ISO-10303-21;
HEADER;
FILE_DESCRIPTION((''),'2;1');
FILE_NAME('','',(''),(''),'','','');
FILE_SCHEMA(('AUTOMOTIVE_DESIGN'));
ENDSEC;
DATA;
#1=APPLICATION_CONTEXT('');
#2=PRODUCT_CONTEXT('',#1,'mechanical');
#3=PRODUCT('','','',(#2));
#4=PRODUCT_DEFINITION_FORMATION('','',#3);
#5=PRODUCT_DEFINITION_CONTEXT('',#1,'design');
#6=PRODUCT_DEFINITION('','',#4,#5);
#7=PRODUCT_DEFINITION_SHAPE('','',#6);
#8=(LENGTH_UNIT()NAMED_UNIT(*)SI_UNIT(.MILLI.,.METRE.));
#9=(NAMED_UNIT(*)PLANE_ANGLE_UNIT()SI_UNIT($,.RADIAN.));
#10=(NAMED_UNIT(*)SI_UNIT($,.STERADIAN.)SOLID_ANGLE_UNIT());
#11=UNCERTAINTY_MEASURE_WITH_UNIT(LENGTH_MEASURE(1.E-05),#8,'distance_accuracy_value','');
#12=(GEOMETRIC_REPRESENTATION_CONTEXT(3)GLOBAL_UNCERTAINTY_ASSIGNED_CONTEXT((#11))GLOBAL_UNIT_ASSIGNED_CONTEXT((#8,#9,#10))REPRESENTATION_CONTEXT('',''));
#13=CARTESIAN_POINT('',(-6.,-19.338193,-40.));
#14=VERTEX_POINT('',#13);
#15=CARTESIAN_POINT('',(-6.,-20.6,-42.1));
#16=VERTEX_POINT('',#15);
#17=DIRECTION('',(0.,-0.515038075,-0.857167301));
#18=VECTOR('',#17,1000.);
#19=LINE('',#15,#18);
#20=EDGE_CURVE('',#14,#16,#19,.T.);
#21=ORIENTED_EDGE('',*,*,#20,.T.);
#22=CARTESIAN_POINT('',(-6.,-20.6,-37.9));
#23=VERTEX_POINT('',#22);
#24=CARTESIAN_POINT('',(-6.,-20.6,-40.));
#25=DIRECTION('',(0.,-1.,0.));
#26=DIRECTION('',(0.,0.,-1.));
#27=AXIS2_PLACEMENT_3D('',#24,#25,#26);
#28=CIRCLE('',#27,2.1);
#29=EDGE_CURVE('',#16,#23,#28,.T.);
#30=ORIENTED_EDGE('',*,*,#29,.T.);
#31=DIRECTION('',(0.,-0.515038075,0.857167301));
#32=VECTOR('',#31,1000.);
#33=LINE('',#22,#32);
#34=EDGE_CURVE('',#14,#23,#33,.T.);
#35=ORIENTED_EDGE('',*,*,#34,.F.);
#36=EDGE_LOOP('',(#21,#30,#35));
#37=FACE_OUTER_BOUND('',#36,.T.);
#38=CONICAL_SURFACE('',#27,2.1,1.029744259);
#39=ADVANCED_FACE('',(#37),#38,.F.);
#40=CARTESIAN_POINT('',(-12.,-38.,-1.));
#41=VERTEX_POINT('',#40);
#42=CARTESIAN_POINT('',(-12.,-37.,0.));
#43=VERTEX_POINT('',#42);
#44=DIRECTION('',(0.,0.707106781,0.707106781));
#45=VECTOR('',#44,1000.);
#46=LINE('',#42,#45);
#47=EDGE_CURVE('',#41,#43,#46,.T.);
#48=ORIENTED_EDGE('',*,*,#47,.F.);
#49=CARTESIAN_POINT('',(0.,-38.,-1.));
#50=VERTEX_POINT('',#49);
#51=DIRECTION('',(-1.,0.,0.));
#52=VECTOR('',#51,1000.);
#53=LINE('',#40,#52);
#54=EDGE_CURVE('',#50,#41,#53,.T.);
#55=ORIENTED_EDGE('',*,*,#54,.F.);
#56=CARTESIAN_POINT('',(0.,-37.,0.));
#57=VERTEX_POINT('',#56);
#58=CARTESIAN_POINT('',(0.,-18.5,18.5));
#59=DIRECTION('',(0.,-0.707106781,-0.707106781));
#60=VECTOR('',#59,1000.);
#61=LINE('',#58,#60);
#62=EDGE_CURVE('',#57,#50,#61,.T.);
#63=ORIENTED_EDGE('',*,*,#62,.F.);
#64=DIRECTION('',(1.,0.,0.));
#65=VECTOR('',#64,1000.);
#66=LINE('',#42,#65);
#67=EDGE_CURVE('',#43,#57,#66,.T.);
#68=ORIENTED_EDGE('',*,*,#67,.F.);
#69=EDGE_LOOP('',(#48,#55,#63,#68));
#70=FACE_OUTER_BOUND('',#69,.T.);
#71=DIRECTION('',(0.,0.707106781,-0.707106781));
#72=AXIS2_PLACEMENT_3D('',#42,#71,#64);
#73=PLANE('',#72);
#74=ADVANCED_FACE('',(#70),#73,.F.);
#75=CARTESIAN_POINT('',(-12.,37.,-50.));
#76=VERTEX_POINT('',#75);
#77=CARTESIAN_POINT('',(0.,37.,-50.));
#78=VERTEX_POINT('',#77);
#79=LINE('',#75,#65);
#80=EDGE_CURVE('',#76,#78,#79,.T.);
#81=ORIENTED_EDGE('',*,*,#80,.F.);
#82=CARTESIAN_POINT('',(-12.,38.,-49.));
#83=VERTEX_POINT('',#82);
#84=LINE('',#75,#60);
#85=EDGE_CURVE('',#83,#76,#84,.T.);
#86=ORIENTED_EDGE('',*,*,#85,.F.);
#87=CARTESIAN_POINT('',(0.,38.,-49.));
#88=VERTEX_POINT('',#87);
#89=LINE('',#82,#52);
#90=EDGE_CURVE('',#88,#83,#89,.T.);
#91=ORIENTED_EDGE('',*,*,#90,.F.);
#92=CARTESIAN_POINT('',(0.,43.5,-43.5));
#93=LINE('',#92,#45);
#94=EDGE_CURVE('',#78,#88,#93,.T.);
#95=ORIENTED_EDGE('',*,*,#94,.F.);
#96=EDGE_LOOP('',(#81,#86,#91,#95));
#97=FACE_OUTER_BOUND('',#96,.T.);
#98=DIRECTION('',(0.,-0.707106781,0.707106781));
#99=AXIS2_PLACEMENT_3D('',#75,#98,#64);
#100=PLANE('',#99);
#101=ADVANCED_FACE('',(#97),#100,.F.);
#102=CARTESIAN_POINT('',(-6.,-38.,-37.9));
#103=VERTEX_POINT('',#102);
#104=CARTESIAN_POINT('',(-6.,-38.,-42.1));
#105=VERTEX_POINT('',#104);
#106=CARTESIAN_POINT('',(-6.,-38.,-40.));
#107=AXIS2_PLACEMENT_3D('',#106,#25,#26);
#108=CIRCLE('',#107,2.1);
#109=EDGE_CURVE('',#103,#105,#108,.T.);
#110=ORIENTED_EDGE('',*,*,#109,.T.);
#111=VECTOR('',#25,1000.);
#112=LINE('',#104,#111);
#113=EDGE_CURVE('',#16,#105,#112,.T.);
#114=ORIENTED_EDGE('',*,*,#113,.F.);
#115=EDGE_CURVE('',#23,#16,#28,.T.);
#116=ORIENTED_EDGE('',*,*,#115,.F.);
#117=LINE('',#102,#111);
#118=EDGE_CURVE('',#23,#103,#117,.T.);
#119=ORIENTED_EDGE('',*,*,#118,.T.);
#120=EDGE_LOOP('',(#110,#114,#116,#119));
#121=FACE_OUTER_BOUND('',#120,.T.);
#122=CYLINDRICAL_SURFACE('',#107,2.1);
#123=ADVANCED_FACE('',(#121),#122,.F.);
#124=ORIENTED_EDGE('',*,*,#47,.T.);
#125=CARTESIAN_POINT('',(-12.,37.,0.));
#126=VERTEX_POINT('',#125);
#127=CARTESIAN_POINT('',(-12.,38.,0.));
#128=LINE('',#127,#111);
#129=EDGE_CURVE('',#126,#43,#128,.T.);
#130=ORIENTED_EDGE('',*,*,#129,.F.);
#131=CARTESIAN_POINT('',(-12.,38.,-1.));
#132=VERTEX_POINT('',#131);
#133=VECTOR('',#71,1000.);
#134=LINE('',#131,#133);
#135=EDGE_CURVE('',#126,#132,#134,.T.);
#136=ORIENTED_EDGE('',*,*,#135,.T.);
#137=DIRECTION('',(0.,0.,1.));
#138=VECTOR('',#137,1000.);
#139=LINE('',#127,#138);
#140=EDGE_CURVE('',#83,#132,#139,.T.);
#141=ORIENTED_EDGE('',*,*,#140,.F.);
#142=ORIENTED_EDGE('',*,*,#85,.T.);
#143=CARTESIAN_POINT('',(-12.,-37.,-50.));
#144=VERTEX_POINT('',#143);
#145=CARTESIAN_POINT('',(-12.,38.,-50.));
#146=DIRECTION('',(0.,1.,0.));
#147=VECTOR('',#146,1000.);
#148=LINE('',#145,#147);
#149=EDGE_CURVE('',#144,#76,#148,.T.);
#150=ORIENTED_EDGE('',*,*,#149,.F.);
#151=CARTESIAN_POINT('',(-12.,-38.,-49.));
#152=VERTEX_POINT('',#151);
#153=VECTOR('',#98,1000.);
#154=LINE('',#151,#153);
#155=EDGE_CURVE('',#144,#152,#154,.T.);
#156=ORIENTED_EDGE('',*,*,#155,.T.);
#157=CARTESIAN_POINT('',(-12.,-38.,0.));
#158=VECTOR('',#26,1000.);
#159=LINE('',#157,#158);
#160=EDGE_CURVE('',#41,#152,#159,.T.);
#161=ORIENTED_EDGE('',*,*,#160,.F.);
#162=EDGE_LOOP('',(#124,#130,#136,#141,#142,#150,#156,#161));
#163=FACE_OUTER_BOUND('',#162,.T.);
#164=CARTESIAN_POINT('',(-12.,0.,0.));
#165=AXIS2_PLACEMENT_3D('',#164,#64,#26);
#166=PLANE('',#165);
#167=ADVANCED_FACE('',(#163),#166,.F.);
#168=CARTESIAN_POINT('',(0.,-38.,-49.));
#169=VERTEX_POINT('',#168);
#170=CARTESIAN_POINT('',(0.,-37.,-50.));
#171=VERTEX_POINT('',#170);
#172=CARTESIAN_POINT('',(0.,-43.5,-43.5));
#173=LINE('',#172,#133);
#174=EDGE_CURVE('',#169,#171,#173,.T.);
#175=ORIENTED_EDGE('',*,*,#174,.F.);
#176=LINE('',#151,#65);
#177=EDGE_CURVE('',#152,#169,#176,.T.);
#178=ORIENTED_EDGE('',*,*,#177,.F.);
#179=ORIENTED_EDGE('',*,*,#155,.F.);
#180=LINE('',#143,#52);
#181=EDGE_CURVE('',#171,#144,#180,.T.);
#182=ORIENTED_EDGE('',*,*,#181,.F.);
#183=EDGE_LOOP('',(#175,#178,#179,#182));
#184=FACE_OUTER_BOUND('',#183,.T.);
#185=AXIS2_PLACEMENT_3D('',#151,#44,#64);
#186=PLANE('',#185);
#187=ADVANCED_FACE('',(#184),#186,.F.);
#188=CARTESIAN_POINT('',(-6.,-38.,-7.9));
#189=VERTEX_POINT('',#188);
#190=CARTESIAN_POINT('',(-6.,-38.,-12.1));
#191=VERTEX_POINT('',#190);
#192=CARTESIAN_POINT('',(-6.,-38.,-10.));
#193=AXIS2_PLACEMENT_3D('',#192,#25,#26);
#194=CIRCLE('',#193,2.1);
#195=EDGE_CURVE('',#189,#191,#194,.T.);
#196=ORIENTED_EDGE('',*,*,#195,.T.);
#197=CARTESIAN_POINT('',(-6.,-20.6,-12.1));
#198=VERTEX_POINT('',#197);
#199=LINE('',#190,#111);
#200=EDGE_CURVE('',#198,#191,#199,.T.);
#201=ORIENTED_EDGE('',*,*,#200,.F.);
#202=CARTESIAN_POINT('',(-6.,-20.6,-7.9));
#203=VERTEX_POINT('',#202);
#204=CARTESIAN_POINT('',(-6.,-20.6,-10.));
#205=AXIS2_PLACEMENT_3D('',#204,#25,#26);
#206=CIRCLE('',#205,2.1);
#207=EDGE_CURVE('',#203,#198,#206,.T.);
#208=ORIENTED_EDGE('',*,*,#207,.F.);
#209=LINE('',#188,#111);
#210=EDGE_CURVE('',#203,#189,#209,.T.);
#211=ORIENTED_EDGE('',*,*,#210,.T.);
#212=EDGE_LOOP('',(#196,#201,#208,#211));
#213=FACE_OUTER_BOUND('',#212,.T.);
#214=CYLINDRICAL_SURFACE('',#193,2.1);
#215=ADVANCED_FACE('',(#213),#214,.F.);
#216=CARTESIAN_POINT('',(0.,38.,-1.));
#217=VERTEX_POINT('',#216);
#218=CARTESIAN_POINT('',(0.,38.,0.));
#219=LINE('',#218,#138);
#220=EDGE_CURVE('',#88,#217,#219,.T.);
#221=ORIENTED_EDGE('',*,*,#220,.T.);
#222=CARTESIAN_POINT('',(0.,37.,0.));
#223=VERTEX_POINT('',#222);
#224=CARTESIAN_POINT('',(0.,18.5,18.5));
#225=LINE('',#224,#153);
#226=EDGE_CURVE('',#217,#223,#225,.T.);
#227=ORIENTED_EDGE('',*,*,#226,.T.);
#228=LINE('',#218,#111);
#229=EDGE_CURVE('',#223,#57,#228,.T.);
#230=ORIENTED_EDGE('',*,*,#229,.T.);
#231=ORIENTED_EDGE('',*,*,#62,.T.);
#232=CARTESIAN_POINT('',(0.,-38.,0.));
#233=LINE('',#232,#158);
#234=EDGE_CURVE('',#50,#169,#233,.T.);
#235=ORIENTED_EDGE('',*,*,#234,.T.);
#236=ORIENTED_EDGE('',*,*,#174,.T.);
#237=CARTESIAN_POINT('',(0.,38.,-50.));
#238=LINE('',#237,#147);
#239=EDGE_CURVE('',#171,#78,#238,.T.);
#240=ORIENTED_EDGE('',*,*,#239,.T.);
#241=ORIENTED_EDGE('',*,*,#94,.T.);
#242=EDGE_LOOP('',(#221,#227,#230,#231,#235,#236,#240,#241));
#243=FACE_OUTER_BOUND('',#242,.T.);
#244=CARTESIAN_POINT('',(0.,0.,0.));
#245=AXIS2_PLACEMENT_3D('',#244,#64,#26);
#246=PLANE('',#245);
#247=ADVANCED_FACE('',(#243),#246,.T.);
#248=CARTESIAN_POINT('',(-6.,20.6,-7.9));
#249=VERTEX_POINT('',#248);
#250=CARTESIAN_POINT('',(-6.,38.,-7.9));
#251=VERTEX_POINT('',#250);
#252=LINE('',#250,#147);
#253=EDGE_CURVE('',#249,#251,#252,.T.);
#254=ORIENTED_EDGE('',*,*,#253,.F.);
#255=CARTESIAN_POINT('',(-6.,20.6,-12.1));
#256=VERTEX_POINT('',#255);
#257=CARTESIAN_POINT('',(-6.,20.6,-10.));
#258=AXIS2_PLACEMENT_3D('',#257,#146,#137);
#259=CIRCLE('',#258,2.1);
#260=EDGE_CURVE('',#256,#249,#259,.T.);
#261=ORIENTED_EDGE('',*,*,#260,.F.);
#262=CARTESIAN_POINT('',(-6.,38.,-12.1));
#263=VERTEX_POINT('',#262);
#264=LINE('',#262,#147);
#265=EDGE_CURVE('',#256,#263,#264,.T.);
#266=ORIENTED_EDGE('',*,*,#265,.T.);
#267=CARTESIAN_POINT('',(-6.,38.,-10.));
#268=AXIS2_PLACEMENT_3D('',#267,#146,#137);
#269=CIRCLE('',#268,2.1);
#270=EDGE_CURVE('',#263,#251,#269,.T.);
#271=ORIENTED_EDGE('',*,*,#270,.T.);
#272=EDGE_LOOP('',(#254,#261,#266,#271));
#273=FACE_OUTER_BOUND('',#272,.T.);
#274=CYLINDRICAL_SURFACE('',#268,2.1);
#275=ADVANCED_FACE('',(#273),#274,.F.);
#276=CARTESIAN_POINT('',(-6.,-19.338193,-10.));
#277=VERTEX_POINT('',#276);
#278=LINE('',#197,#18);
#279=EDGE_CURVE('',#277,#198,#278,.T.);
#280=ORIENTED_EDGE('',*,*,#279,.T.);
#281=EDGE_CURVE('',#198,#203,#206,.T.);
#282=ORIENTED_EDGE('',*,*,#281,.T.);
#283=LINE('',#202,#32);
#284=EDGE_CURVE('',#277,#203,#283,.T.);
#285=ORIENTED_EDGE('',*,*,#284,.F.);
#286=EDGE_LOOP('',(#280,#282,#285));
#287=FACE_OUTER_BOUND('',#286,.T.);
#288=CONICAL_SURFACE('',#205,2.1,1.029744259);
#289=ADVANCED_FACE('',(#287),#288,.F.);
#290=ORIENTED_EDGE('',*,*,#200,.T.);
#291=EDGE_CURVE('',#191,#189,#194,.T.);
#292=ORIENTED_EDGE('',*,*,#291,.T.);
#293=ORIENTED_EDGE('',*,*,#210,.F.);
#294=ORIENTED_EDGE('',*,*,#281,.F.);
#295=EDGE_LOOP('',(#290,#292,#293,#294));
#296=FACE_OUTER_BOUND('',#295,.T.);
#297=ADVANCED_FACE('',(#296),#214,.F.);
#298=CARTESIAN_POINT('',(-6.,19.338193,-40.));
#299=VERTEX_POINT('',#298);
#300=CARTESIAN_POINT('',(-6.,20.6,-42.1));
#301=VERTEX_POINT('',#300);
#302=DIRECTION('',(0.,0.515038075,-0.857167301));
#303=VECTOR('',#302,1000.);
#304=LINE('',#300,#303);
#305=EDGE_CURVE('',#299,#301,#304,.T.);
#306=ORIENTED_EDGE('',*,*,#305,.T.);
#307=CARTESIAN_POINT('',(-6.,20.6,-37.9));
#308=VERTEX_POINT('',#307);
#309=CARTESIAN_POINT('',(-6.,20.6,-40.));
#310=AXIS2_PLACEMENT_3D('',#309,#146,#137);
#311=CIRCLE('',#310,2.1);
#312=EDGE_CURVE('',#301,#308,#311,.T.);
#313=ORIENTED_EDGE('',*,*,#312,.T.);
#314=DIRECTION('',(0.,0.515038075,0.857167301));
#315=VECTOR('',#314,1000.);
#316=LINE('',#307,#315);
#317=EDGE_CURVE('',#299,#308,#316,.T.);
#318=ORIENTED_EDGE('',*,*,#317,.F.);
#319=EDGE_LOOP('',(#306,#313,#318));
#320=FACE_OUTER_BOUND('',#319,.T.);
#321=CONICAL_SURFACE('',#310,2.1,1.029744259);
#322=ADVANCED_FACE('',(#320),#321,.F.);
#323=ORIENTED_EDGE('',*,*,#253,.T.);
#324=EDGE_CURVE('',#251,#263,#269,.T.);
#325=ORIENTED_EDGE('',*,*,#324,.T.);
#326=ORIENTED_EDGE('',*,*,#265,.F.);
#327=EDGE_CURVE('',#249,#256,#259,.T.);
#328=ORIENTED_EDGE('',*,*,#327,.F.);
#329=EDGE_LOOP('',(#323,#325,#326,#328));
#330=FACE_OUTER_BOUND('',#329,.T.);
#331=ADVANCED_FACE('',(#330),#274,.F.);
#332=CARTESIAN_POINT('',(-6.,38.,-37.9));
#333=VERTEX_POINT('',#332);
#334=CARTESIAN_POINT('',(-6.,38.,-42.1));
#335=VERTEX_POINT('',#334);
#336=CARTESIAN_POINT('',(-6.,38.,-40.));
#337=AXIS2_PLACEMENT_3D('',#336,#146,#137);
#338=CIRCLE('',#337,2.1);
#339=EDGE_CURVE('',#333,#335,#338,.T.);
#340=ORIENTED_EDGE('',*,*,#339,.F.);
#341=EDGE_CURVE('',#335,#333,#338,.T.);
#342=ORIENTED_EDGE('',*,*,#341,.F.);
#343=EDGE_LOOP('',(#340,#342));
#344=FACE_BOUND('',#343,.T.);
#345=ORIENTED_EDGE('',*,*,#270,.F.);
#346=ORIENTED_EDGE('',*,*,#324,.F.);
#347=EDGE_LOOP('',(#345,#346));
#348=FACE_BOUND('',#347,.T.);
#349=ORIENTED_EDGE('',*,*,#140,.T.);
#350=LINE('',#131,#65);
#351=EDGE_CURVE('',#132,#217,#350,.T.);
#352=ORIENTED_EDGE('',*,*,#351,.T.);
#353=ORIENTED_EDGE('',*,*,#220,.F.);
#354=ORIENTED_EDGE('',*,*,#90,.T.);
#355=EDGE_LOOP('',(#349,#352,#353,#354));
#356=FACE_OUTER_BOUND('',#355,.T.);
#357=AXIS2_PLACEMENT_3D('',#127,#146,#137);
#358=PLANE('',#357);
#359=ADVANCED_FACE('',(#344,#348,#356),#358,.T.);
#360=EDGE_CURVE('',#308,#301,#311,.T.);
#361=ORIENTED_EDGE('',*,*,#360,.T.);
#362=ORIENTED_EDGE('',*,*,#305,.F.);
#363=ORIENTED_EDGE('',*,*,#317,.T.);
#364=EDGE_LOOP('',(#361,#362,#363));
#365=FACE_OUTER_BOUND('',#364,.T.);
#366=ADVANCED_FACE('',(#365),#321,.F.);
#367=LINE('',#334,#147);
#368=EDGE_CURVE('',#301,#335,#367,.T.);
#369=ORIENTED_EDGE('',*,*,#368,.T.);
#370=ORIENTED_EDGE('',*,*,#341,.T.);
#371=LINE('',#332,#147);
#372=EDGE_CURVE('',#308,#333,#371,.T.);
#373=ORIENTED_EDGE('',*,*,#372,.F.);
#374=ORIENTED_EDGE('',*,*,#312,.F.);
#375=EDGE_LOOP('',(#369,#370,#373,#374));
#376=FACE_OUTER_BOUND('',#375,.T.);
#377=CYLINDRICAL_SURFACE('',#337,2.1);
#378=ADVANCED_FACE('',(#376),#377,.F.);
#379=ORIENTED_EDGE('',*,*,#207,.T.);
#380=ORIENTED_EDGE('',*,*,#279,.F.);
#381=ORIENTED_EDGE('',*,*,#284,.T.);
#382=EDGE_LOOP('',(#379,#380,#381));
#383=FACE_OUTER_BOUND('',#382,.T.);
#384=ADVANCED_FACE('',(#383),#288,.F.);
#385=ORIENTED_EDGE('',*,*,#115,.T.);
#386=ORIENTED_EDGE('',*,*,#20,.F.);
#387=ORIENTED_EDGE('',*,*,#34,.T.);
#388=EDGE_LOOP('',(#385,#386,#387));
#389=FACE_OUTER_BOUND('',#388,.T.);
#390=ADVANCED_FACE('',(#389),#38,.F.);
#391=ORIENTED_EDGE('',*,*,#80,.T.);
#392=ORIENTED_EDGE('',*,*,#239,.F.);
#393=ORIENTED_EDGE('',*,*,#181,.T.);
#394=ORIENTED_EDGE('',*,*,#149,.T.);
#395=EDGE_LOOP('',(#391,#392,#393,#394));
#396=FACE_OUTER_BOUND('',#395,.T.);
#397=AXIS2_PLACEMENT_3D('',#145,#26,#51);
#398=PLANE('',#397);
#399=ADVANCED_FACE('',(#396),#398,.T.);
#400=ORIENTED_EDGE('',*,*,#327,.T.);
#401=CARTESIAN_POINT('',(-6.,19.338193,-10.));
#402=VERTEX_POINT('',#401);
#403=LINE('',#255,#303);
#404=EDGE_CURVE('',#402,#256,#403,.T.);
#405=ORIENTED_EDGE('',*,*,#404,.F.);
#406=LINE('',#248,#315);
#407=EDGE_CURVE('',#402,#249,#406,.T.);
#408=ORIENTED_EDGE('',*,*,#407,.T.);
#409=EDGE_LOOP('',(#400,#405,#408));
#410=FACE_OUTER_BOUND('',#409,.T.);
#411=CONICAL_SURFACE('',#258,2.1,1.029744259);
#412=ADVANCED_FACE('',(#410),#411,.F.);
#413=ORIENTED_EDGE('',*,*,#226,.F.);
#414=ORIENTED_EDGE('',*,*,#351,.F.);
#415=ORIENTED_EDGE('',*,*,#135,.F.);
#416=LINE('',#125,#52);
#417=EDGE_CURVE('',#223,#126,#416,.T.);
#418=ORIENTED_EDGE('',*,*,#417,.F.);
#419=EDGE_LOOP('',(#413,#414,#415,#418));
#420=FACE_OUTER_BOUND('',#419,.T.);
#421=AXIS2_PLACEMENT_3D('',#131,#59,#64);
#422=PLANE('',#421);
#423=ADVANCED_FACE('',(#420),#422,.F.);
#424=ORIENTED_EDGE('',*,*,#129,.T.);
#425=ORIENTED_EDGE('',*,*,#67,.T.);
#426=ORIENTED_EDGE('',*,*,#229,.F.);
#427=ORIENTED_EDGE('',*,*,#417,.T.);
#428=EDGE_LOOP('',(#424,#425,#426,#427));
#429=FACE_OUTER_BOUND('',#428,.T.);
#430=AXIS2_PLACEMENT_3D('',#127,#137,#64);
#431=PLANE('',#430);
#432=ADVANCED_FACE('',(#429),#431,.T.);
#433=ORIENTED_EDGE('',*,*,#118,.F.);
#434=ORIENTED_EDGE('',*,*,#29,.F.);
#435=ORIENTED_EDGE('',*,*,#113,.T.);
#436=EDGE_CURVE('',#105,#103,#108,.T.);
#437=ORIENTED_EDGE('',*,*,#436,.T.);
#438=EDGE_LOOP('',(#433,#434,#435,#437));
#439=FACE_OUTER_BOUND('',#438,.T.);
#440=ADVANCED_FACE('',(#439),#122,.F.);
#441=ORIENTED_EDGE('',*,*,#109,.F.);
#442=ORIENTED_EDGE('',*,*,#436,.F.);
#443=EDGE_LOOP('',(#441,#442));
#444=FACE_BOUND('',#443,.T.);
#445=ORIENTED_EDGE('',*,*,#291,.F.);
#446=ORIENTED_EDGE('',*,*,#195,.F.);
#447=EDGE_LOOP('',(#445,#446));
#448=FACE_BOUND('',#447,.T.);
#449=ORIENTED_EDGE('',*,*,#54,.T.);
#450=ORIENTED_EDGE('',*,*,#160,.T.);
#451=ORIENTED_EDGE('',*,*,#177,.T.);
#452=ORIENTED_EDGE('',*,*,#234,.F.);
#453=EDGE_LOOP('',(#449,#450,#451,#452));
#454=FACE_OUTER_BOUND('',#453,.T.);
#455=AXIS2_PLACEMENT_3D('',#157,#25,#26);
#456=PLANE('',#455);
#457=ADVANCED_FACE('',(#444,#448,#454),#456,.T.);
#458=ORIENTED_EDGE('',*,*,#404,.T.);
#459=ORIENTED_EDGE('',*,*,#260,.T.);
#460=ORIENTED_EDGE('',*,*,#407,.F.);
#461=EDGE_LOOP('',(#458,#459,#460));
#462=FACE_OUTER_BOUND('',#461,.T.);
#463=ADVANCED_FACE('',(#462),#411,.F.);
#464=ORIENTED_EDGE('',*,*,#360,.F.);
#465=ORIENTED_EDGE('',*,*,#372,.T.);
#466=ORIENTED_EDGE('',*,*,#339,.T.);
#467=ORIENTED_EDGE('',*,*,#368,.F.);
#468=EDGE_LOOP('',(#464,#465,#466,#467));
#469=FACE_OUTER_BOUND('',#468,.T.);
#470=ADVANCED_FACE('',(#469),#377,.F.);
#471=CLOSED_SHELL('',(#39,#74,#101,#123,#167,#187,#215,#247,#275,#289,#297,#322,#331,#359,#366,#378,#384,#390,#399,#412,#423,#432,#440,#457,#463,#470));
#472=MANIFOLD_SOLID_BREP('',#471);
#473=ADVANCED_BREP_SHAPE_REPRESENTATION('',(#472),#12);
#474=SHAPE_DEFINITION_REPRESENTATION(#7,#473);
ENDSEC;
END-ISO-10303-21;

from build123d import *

# Parameters (mm, degrees)
SKETCH6_W                  = 50
SKETCH6_H                  = 76
BOSS_EXTRUDE6_DEPTH        = 12
M5_TAPPED_HOLE3_AT_2_COUNT = 2
M5_TAPPED_HOLE3_AT_2_PITCH = 30
CHAMFER1_SIZE              = 1


with BuildPart() as part:
    # Sketch6 → Boss-Extrude6 (new body)
    with BuildSketch(Plane(origin=(0, 0, 0), x_dir=(0, 0, -1), z_dir=(1, 0, 0))):
        with Locations((25, 0)):
            Rectangle(SKETCH6_W, SKETCH6_H)
    extrude(amount=-BOSS_EXTRUDE6_DEPTH)

    # Sketch19 → M5 Tapped Hole3 (revolve, cut)
    with BuildSketch(Plane(origin=(-6, -38, -10), x_dir=(0, 0, -1), z_dir=(1, 0, 0))):
        Polygon((0, 0), (0, 18.6618073), (2.1, 17.4), (2.1, 0), align=None)
    m5_tapped_hole3 = revolve(axis=Axis((-6, -44.35, -10), (0, 1, 0)), mode=Mode.SUBTRACT)

    # M5 Tapped Hole3 at 2: M5 Tapped Hole3 ×2
    with Locations(*[(0, 0, -i * M5_TAPPED_HOLE3_AT_2_PITCH) for i in range(1, M5_TAPPED_HOLE3_AT_2_COUNT)]):
        add(m5_tapped_hole3, mode=Mode.SUBTRACT)

    # Mirror1: M5 Tapped Hole3 across plane
    add(m5_tapped_hole3.mirror(Plane.ZX), mode=Mode.SUBTRACT)

    # Mirror1 copy 1 sketch → Mirror1 copy 1 (revolve, cut)
    with BuildSketch(Plane(origin=(-6, 38, -40), x_dir=(0, 0, -1), z_dir=(1, 0, 0))):
        Polygon((0, 0), (0, -18.6618073), (2.1, -17.4), (2.1, 0), align=None)
    revolve(axis=Axis((-6, 44.35, -40), (0, 1, 0)), mode=Mode.SUBTRACT)

    # Chamfer1
    chamfer1_edges = [part.edges().sort_by_distance(p)[0] for p in [
        (-6, 38, 0),
        (-6, 38, -50),
        (-6, -38, -50),
        (-6, -38, 0),
    ]]
    chamfer(chamfer1_edges, length=CHAMFER1_SIZE)


solid = part.part
